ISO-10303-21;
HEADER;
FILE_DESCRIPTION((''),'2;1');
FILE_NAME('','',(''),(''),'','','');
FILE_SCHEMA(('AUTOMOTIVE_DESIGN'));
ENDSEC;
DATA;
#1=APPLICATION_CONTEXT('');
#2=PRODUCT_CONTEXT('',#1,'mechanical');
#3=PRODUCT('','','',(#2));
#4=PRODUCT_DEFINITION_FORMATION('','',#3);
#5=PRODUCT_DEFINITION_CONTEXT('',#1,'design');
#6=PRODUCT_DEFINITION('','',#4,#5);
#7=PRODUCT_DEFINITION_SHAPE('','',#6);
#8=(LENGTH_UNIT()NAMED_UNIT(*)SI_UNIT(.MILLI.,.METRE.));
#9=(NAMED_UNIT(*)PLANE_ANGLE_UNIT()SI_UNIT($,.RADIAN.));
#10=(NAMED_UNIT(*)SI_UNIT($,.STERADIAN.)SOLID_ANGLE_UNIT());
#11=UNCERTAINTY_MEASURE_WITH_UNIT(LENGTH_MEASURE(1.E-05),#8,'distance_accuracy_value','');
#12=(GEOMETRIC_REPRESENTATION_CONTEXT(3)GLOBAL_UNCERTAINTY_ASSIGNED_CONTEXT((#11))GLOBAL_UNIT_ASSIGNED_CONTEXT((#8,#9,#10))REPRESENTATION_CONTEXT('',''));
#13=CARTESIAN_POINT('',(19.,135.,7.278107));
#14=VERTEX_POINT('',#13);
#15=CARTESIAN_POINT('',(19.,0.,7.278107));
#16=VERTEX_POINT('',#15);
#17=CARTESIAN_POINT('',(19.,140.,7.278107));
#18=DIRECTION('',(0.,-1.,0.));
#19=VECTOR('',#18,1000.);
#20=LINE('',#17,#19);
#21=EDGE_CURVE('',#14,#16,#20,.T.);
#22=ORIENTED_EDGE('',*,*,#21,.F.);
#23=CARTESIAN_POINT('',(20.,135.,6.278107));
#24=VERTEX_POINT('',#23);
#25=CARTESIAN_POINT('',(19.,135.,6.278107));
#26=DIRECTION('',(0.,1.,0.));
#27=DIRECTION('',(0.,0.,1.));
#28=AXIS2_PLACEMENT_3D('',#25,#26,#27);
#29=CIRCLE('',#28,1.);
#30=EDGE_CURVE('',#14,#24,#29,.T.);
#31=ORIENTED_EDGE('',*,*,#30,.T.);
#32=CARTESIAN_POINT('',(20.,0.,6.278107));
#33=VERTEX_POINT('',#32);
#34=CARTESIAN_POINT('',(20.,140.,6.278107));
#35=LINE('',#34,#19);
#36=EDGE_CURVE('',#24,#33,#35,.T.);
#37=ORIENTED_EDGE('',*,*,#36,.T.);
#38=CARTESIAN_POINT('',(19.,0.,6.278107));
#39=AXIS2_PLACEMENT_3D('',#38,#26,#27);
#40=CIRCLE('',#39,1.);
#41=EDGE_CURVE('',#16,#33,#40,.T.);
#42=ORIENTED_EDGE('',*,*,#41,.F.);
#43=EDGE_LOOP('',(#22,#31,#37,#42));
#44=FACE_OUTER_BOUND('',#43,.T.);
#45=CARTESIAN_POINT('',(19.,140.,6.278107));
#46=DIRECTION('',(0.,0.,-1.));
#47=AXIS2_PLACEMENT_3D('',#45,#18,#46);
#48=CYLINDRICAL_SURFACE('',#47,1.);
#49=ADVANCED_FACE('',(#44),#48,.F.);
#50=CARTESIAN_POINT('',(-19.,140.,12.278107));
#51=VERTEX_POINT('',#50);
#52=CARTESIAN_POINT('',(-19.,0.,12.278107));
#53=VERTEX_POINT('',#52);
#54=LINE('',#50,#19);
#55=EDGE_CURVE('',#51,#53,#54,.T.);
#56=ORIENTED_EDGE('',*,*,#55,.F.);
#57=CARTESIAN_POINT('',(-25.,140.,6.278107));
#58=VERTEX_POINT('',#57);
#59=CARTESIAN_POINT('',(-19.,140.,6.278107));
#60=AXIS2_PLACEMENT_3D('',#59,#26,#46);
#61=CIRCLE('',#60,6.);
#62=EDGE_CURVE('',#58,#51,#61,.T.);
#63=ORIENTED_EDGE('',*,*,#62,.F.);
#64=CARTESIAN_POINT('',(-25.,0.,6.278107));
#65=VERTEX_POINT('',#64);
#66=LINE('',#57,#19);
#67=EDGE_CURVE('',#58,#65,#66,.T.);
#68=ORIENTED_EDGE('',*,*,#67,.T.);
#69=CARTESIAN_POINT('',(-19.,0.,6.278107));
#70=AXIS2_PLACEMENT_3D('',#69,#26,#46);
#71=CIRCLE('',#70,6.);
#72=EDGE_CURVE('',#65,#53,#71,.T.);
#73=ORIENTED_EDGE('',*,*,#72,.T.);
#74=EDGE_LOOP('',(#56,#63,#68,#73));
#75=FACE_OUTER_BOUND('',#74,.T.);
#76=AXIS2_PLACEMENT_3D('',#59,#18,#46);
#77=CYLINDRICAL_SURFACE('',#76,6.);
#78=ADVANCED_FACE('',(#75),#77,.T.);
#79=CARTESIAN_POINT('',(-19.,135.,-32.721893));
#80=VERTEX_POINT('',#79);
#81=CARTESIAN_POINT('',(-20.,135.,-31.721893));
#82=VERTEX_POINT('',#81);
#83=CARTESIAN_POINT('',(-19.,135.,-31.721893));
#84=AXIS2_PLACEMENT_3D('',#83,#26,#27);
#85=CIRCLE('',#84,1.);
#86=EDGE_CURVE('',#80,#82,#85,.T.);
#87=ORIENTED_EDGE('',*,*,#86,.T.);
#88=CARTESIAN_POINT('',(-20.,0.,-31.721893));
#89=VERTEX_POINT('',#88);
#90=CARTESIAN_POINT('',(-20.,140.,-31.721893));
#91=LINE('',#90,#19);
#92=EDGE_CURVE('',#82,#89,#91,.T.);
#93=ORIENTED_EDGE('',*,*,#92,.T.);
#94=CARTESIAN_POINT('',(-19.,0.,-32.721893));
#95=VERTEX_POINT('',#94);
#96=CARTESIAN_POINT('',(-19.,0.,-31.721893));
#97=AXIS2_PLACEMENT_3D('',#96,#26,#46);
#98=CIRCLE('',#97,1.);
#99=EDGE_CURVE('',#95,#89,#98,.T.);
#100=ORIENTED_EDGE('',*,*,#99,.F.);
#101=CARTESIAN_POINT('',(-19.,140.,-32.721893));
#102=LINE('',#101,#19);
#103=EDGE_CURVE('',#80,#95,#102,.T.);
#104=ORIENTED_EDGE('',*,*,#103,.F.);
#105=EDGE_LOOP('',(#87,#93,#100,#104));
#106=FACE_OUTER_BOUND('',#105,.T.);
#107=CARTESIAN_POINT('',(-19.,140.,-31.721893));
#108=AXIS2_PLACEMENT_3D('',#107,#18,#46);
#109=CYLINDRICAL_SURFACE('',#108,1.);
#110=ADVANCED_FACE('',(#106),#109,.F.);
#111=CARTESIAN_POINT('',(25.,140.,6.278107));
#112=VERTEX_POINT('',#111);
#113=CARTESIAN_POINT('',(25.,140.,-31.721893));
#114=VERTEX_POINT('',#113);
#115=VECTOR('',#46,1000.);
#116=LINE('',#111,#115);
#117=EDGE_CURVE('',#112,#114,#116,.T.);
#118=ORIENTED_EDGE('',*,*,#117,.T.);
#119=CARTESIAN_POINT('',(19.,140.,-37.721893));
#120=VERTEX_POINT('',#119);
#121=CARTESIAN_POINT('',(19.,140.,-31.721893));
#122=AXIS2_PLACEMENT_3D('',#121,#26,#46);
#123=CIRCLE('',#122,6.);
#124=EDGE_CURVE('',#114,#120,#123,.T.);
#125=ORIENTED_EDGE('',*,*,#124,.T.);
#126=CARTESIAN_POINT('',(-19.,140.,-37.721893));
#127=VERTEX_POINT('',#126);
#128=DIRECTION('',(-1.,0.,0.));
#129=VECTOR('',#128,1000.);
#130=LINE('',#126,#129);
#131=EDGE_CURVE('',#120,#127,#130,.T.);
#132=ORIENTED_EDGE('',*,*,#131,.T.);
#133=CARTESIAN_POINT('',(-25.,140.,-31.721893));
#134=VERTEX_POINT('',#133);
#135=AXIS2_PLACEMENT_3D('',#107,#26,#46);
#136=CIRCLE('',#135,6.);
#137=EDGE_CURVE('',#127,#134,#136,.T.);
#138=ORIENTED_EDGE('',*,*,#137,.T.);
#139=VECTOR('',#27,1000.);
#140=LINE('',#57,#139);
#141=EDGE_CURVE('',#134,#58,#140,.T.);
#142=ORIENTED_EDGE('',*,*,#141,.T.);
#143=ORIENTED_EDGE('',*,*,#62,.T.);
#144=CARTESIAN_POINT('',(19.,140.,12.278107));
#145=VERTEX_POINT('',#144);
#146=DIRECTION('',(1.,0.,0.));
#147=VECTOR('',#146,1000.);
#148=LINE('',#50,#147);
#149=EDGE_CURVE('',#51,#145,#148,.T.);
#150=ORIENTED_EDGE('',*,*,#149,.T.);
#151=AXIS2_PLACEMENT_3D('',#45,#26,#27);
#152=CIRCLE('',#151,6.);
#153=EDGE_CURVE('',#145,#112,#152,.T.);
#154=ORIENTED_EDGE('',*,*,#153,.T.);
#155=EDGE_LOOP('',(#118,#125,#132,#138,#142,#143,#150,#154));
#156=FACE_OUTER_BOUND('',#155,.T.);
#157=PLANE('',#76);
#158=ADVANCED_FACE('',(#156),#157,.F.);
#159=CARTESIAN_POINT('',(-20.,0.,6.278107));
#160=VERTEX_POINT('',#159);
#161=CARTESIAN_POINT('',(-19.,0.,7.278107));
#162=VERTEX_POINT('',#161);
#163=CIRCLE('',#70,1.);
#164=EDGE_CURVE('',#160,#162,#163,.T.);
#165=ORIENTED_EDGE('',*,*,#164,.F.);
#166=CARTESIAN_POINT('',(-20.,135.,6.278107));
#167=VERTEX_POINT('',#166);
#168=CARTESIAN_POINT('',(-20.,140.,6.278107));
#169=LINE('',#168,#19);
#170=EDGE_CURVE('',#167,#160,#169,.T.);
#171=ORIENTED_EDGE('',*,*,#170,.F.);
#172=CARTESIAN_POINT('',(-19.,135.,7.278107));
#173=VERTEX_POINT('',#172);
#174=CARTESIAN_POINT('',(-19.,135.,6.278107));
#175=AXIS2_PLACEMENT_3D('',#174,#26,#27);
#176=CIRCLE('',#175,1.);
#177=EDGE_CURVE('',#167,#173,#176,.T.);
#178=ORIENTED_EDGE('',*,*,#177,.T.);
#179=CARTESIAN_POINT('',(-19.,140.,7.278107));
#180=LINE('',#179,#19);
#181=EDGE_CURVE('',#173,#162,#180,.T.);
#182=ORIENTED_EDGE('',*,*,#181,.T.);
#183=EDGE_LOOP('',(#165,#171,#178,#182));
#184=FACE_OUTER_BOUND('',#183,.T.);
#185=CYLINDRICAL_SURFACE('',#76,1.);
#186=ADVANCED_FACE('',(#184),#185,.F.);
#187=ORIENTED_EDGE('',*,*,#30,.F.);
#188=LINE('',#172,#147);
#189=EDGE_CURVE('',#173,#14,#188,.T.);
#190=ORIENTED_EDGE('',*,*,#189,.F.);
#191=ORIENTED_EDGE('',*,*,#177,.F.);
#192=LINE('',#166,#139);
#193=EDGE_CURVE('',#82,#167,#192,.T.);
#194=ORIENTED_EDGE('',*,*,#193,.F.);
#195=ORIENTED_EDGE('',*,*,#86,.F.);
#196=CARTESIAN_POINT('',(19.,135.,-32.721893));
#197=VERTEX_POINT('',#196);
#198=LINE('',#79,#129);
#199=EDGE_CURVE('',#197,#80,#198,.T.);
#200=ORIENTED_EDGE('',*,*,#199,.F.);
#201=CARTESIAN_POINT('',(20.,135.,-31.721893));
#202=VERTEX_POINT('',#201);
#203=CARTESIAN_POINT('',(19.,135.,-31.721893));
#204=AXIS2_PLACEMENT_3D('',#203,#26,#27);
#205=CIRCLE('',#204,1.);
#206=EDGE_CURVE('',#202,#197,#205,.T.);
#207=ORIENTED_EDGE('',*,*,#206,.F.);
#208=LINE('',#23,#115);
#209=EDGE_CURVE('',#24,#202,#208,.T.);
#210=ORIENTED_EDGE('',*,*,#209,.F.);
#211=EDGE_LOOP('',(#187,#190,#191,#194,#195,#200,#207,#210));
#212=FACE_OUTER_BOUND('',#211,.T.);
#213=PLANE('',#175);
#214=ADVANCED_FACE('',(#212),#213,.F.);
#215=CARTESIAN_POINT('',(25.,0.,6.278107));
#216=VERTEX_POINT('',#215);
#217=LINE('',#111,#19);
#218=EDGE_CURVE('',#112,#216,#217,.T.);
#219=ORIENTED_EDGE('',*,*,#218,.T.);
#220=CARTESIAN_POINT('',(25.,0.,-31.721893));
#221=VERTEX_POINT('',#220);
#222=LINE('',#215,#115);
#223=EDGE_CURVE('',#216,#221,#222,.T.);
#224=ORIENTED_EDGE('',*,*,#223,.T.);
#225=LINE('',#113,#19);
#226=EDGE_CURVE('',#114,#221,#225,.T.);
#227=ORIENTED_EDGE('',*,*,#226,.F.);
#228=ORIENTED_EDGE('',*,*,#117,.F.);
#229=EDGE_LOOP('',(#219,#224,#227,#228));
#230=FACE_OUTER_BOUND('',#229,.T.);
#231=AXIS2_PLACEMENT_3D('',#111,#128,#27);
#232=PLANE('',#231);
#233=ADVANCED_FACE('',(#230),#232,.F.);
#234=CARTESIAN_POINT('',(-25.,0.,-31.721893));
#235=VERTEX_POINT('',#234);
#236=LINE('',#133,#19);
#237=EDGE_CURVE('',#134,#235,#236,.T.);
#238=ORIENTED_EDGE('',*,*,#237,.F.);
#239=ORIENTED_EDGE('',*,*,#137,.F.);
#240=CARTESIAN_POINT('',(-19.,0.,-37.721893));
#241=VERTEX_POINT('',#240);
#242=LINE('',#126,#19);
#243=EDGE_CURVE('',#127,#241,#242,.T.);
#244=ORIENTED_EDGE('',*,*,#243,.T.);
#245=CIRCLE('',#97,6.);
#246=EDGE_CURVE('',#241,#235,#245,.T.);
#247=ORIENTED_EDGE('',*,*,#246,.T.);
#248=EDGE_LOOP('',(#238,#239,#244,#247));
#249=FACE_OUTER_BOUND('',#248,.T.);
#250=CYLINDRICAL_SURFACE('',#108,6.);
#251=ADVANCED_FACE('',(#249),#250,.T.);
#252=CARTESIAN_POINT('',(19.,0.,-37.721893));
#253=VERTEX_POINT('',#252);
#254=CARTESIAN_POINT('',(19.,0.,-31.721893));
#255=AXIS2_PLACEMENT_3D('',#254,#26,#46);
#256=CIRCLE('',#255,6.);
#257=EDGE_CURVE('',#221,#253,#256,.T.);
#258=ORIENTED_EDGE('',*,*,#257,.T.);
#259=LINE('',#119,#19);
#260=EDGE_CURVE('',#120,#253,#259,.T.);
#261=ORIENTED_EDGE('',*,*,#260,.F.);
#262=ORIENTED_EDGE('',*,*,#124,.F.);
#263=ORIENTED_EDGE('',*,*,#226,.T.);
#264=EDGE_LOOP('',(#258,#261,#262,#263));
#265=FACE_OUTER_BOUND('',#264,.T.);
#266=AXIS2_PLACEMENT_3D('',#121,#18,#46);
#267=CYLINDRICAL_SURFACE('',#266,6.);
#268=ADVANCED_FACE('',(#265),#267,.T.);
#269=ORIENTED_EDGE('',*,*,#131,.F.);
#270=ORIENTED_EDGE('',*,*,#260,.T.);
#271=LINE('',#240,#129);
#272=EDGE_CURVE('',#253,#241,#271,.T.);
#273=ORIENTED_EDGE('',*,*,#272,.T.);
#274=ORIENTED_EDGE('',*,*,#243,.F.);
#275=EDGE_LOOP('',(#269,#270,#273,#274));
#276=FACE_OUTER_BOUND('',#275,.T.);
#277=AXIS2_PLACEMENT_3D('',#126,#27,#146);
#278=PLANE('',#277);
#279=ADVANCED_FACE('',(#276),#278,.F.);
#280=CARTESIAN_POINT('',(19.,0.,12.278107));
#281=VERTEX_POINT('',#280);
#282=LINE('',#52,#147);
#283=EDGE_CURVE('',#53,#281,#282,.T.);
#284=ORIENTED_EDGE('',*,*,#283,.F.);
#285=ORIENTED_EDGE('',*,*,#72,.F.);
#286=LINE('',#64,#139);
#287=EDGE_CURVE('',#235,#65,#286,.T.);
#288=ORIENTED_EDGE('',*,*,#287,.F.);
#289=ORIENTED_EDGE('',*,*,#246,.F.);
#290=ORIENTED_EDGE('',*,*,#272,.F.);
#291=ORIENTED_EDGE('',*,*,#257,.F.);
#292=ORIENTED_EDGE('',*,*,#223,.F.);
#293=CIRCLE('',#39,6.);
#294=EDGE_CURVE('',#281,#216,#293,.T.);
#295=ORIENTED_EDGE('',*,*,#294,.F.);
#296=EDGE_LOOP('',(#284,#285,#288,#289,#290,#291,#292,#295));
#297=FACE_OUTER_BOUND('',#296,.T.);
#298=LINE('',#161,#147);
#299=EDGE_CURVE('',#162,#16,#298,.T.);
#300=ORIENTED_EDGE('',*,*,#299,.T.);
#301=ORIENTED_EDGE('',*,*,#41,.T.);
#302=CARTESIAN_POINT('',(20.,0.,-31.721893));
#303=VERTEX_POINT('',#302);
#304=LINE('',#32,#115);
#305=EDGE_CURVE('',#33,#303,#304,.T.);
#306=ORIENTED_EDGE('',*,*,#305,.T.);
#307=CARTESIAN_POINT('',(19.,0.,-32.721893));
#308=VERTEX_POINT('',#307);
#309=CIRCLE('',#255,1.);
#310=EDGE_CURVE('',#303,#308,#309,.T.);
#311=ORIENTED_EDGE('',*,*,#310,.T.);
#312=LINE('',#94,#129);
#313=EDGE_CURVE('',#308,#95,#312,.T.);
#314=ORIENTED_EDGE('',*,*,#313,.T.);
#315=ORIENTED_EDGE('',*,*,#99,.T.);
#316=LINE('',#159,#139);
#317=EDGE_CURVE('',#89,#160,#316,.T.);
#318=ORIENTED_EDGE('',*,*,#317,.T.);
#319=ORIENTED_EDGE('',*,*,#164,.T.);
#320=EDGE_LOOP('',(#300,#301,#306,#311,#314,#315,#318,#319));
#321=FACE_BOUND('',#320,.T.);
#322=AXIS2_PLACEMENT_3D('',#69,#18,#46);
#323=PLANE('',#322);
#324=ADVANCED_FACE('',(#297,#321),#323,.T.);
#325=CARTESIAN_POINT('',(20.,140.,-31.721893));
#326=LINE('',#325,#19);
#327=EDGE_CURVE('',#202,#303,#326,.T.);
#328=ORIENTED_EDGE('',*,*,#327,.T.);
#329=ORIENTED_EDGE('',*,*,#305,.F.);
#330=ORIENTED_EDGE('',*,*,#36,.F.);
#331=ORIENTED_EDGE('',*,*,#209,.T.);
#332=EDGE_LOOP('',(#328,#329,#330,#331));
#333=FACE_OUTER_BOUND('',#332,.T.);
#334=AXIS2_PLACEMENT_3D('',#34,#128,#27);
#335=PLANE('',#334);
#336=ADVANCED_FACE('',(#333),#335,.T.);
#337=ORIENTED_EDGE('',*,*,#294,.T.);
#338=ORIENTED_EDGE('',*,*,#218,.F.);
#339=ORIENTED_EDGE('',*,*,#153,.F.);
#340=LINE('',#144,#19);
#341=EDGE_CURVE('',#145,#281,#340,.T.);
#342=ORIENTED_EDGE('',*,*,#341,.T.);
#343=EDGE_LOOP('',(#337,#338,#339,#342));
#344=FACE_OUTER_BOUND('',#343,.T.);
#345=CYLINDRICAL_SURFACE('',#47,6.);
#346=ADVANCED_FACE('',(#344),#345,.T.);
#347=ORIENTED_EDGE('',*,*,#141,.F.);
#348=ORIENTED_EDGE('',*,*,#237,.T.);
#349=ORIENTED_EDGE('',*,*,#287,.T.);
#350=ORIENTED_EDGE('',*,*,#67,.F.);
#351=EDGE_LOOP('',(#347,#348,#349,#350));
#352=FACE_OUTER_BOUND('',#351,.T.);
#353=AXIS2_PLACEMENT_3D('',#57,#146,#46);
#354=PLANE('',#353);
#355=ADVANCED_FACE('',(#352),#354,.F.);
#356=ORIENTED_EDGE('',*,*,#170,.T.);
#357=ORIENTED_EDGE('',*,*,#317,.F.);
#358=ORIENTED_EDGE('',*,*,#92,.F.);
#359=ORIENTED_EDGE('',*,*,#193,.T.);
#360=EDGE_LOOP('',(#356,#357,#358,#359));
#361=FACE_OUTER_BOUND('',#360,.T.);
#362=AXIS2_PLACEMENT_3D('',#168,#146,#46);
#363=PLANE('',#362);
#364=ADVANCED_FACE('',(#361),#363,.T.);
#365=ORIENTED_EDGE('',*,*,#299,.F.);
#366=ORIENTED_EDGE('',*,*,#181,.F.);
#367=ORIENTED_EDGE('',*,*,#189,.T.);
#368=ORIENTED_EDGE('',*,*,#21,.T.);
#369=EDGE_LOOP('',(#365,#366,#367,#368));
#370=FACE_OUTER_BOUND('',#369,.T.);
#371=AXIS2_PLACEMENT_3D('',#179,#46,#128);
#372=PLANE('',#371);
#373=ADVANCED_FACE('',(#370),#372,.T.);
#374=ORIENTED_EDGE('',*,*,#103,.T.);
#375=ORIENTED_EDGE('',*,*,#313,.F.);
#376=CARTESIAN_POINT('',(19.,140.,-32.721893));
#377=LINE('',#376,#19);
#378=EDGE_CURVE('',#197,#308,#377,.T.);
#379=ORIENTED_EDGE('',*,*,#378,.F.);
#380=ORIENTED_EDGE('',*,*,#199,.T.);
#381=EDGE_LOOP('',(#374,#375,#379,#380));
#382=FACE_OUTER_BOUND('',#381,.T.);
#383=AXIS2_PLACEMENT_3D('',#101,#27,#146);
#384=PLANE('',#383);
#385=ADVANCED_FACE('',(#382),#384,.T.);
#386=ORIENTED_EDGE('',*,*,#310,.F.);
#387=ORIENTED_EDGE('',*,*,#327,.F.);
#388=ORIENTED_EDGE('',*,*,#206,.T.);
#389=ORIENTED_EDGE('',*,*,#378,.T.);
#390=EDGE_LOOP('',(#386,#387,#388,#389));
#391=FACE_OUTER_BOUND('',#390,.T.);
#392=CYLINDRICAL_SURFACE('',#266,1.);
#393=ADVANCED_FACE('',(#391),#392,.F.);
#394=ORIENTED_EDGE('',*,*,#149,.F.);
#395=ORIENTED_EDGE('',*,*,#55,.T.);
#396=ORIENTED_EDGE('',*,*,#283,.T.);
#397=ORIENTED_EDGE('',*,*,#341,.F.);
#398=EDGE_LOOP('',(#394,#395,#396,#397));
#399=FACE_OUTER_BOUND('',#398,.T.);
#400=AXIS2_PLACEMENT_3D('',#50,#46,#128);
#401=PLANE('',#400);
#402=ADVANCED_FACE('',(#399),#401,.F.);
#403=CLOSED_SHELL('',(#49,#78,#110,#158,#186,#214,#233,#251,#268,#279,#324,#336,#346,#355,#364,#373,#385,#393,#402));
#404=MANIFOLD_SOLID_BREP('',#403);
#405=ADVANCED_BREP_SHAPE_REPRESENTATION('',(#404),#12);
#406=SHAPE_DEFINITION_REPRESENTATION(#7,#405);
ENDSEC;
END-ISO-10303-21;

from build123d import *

# Parameters (mm, degrees)
EXTRUDE_1_DEPTH = 140
EXTRUDE_START   = -5
EXTRUDE_2_DEPTH = 5


with BuildPart() as part:
    # 草图1 → 凸台-拉伸1 (new body)
    with BuildSketch(Plane(origin=(0, 0, 0), x_dir=(1, 0, 0), z_dir=(0, 1, 0))):
        with BuildLine():
            Line((-19, -12.278106509), (19, -12.278106509))
            ThreePointArc((19, -12.278106509), (23.242640687, -10.520747196), (25, -6.278106509))
            Line((25, -6.278106509), (25, 31.721893491))
            ThreePointArc((25, 31.721893491), (23.242640687, 35.964534178), (19, 37.721893491))
            Line((19, 37.721893491), (-19, 37.721893491))
            ThreePointArc((-19, 37.721893491), (-23.242640687, 35.964534178), (-25, 31.721893491))
            Line((-25, 31.721893491), (-25, -6.278106509))
            ThreePointArc((-25, -6.278106509), (-23.242640687, -10.520747196), (-19, -12.278106509))
        make_face()
        with BuildLine():
            Line((-19, -7.278106509), (19, -7.278106509))
            ThreePointArc((19, -7.278106509), (19.707106781, -6.98521329), (20, -6.278106509))
            Line((20, -6.278106509), (20, 31.721893491))
            ThreePointArc((20, 31.721893491), (19.707106781, 32.429000272), (19, 32.721893491))
            Line((19, 32.721893491), (-19, 32.721893491))
            ThreePointArc((-19, 32.721893491), (-19.707106781, 32.429000272), (-20, 31.721893491))
            Line((-20, 31.721893491), (-20, -6.278106509))
            ThreePointArc((-20, -6.278106509), (-19.707106781, -6.98521329), (-19, -7.278106509))
        make_face(mode=Mode.SUBTRACT)
    extrude(amount=EXTRUDE_1_DEPTH)

    # 草图2 → 凸台-拉伸2 (add)
    with BuildSketch(Plane(origin=(0, 140, 0), x_dir=(1, 0, 0), z_dir=(0, 1, 0)).offset(EXTRUDE_START)):
        with BuildLine():
            Line((-19, -12.278106509), (19, -12.278106509))
            ThreePointArc((19, -12.278106509), (23.242640687, -10.520747196), (25, -6.278106509))
            Line((25, -6.278106509), (25, 31.721893491))
            ThreePointArc((25, 31.721893491), (23.242640687, 35.964534178), (19, 37.721893491))
            Line((19, 37.721893491), (-19, 37.721893491))
            ThreePointArc((-19, 37.721893491), (-23.242640687, 35.964534178), (-25, 31.721893491))
            Line((-25, 31.721893491), (-25, -6.278106509))
            ThreePointArc((-25, -6.278106509), (-23.242640687, -10.520747196), (-19, -12.278106509))
        make_face()
    extrude(amount=EXTRUDE_2_DEPTH)


solid = part.part
